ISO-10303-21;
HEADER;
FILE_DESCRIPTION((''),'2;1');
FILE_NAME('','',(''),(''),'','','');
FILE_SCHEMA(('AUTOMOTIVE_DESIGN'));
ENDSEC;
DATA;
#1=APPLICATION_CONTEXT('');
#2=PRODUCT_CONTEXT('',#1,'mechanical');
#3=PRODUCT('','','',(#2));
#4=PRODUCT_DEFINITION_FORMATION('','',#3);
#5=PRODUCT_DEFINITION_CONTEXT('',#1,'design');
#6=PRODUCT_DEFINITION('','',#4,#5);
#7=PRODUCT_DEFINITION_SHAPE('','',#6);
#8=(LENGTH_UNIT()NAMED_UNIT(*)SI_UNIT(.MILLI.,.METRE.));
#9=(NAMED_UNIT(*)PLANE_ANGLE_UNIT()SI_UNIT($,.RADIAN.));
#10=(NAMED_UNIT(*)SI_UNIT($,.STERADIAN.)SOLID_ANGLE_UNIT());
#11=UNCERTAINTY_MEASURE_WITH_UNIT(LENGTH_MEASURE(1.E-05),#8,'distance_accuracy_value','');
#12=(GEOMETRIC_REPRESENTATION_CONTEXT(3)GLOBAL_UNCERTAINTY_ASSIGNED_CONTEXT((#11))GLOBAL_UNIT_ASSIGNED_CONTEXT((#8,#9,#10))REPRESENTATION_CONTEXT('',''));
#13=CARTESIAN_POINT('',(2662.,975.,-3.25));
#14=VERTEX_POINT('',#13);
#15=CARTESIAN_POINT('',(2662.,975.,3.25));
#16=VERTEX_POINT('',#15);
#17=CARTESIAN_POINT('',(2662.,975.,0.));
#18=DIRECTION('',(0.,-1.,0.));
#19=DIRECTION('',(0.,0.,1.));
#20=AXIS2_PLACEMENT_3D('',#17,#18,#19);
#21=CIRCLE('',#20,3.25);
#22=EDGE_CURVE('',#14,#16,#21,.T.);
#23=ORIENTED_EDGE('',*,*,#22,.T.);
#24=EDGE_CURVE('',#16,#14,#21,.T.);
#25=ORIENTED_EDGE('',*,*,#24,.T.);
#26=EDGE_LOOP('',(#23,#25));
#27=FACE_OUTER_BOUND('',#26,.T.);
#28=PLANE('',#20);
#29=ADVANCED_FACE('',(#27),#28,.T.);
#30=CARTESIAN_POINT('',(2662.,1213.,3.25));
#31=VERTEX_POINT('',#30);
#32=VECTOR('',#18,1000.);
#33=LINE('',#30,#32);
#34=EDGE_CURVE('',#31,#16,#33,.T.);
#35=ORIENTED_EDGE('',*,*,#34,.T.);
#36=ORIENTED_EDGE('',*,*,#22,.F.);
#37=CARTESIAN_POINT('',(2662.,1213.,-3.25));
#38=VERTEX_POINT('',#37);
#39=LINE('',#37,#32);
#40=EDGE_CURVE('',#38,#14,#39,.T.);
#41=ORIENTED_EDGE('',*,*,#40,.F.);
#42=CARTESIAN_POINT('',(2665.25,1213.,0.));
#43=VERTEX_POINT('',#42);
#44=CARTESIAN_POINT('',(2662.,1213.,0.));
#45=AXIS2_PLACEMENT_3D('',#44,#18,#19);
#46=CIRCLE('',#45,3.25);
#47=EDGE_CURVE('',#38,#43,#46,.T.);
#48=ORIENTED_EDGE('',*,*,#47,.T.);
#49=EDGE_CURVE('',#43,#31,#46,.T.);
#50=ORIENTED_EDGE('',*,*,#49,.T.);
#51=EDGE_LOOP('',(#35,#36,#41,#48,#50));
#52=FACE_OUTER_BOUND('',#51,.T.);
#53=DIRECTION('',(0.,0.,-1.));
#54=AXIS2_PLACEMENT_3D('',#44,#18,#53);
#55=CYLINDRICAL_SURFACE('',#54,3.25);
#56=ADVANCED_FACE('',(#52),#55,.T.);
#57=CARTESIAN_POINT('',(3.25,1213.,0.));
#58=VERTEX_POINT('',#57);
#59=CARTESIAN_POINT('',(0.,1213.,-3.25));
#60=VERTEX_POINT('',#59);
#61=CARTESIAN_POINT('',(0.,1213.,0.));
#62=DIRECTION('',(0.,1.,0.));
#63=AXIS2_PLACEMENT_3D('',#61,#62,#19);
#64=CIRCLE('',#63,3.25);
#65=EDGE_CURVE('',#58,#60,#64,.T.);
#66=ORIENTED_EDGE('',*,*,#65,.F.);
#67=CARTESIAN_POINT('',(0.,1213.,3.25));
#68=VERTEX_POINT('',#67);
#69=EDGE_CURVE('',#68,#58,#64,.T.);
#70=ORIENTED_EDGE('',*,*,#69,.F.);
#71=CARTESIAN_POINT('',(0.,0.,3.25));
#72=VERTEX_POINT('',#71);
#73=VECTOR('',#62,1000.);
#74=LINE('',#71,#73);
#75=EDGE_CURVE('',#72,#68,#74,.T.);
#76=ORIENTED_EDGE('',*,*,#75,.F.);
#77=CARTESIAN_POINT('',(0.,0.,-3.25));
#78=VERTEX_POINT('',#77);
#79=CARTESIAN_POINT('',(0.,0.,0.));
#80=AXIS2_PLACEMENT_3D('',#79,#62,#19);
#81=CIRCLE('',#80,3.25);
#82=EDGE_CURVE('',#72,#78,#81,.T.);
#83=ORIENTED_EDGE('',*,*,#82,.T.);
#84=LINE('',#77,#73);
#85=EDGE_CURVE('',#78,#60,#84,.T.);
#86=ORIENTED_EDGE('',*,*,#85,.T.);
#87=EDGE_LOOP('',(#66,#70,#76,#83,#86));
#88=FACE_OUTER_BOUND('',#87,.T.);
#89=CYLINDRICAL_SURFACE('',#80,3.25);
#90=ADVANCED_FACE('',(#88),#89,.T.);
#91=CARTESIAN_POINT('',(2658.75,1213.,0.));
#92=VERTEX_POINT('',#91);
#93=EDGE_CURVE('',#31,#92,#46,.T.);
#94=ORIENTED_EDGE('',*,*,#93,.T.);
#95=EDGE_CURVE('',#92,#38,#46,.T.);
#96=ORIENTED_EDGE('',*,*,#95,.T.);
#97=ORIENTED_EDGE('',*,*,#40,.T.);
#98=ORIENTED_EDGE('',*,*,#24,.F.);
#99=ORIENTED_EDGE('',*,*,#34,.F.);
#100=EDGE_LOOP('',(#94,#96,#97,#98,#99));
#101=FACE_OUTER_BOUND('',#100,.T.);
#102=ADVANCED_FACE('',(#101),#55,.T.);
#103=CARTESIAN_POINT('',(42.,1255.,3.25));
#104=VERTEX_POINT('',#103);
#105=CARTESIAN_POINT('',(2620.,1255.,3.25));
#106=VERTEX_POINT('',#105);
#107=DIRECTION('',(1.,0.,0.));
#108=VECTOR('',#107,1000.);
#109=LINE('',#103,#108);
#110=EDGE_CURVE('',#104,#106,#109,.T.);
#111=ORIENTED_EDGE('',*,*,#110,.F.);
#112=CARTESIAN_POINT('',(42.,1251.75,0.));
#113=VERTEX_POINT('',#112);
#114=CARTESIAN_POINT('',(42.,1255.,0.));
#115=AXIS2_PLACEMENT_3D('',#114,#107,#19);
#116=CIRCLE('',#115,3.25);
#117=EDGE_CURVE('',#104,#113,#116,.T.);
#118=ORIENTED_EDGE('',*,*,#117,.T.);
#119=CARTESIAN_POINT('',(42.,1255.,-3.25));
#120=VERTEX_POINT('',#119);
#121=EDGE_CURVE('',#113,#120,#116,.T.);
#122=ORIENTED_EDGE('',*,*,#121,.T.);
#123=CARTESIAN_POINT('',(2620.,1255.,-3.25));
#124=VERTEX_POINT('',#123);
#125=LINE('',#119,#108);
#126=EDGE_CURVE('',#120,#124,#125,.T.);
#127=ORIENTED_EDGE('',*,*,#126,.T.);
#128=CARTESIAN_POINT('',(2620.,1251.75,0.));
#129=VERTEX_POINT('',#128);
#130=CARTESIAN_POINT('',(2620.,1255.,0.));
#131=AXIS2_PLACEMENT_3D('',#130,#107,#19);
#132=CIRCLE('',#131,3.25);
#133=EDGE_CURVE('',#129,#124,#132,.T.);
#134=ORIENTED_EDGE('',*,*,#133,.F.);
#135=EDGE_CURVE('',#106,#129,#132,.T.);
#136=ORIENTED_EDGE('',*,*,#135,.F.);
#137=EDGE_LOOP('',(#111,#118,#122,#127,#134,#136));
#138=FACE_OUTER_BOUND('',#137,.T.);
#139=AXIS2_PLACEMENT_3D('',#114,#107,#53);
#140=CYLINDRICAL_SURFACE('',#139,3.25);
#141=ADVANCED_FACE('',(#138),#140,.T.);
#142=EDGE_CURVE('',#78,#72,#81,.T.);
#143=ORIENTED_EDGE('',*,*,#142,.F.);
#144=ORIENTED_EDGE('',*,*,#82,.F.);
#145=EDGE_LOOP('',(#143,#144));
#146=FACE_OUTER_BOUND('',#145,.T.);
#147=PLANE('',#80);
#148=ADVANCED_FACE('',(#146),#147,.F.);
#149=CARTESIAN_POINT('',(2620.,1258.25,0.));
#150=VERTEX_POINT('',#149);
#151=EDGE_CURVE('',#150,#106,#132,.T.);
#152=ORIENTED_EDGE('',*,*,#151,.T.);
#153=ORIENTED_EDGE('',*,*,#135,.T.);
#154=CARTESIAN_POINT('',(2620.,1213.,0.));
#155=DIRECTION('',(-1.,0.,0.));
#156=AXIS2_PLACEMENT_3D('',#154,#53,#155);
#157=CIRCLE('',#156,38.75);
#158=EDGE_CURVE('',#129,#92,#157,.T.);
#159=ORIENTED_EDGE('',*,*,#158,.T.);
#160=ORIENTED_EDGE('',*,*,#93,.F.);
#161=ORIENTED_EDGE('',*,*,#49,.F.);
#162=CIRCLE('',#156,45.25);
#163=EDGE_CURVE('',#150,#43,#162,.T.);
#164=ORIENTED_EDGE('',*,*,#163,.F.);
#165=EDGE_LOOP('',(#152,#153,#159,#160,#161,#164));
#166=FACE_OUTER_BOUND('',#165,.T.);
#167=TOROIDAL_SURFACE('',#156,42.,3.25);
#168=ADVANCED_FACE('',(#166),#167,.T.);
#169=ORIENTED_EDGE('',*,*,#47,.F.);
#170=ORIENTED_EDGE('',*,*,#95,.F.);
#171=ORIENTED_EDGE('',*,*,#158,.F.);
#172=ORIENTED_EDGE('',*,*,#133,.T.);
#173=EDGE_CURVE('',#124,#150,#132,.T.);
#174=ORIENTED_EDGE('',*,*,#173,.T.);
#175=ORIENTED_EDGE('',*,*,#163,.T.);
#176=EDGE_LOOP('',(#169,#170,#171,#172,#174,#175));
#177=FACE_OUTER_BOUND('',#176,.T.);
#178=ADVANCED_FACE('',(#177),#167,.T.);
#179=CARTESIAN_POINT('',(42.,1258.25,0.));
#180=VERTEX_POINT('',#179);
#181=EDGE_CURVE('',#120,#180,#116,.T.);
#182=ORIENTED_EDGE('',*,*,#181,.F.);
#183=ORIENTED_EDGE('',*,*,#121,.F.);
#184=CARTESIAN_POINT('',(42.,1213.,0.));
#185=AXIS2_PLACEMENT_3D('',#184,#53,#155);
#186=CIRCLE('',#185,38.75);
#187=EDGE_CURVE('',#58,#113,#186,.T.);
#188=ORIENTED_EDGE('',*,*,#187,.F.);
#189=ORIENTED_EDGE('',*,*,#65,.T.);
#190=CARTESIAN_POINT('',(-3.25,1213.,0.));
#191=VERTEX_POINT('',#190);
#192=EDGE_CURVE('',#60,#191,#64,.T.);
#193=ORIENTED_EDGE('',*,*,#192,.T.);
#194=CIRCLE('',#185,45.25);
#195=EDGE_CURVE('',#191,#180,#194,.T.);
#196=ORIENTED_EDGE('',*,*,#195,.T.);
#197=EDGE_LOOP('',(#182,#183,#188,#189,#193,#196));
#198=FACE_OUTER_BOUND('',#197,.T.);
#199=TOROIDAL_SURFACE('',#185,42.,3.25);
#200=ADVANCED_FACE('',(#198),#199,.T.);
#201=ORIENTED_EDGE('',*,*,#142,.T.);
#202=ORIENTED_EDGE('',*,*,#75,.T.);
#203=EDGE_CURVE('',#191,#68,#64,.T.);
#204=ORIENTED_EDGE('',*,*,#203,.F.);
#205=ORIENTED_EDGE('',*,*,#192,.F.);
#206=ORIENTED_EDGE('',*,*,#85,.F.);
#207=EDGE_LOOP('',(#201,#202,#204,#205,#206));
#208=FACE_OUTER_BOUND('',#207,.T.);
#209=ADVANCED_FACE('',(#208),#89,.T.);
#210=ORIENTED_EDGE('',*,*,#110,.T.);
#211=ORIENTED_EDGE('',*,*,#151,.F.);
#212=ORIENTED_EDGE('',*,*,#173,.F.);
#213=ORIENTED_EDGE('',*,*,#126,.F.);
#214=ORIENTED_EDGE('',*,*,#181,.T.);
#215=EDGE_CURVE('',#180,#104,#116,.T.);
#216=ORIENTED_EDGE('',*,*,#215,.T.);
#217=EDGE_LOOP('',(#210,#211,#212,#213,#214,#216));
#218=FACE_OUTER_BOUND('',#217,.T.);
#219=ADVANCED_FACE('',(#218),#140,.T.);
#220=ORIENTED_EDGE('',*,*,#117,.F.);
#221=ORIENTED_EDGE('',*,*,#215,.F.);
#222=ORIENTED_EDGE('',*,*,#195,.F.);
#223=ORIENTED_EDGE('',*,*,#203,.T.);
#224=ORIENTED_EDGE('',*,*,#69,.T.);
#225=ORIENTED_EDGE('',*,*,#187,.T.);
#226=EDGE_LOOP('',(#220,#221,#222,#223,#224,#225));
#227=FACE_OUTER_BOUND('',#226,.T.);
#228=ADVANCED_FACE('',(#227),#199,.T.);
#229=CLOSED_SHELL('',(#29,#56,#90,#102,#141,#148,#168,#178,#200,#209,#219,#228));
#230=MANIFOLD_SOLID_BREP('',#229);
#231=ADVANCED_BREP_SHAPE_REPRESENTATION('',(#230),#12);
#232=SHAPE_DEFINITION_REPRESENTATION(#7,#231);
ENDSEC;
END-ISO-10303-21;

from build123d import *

# Parameters (mm, degrees)
SKETCH2_R = 3.25


with BuildPart() as part:
    # Sweep1: sweep along a path in Sketch1
    with BuildLine(Plane.XY) as sweep1_path:
        Line((0, 0), (0, 1213))
        ThreePointArc((0, 1213), (12.30151519, 1242.69848481), (42, 1255))
        Line((42, 1255), (2620, 1255))
        ThreePointArc((2620, 1255), (2649.69848481, 1242.69848481), (2662, 1213))
        Line((2662, 1213), (2662, 975))
    # Sketch2 → Sweep1 (sweep)
    with BuildSketch(Plane(origin=(0, 0, 0), x_dir=(1, 0, 0), z_dir=(0, 1, 0))):
        Circle(SKETCH2_R)
    sweep(path=sweep1_path.line)


solid = part.part
